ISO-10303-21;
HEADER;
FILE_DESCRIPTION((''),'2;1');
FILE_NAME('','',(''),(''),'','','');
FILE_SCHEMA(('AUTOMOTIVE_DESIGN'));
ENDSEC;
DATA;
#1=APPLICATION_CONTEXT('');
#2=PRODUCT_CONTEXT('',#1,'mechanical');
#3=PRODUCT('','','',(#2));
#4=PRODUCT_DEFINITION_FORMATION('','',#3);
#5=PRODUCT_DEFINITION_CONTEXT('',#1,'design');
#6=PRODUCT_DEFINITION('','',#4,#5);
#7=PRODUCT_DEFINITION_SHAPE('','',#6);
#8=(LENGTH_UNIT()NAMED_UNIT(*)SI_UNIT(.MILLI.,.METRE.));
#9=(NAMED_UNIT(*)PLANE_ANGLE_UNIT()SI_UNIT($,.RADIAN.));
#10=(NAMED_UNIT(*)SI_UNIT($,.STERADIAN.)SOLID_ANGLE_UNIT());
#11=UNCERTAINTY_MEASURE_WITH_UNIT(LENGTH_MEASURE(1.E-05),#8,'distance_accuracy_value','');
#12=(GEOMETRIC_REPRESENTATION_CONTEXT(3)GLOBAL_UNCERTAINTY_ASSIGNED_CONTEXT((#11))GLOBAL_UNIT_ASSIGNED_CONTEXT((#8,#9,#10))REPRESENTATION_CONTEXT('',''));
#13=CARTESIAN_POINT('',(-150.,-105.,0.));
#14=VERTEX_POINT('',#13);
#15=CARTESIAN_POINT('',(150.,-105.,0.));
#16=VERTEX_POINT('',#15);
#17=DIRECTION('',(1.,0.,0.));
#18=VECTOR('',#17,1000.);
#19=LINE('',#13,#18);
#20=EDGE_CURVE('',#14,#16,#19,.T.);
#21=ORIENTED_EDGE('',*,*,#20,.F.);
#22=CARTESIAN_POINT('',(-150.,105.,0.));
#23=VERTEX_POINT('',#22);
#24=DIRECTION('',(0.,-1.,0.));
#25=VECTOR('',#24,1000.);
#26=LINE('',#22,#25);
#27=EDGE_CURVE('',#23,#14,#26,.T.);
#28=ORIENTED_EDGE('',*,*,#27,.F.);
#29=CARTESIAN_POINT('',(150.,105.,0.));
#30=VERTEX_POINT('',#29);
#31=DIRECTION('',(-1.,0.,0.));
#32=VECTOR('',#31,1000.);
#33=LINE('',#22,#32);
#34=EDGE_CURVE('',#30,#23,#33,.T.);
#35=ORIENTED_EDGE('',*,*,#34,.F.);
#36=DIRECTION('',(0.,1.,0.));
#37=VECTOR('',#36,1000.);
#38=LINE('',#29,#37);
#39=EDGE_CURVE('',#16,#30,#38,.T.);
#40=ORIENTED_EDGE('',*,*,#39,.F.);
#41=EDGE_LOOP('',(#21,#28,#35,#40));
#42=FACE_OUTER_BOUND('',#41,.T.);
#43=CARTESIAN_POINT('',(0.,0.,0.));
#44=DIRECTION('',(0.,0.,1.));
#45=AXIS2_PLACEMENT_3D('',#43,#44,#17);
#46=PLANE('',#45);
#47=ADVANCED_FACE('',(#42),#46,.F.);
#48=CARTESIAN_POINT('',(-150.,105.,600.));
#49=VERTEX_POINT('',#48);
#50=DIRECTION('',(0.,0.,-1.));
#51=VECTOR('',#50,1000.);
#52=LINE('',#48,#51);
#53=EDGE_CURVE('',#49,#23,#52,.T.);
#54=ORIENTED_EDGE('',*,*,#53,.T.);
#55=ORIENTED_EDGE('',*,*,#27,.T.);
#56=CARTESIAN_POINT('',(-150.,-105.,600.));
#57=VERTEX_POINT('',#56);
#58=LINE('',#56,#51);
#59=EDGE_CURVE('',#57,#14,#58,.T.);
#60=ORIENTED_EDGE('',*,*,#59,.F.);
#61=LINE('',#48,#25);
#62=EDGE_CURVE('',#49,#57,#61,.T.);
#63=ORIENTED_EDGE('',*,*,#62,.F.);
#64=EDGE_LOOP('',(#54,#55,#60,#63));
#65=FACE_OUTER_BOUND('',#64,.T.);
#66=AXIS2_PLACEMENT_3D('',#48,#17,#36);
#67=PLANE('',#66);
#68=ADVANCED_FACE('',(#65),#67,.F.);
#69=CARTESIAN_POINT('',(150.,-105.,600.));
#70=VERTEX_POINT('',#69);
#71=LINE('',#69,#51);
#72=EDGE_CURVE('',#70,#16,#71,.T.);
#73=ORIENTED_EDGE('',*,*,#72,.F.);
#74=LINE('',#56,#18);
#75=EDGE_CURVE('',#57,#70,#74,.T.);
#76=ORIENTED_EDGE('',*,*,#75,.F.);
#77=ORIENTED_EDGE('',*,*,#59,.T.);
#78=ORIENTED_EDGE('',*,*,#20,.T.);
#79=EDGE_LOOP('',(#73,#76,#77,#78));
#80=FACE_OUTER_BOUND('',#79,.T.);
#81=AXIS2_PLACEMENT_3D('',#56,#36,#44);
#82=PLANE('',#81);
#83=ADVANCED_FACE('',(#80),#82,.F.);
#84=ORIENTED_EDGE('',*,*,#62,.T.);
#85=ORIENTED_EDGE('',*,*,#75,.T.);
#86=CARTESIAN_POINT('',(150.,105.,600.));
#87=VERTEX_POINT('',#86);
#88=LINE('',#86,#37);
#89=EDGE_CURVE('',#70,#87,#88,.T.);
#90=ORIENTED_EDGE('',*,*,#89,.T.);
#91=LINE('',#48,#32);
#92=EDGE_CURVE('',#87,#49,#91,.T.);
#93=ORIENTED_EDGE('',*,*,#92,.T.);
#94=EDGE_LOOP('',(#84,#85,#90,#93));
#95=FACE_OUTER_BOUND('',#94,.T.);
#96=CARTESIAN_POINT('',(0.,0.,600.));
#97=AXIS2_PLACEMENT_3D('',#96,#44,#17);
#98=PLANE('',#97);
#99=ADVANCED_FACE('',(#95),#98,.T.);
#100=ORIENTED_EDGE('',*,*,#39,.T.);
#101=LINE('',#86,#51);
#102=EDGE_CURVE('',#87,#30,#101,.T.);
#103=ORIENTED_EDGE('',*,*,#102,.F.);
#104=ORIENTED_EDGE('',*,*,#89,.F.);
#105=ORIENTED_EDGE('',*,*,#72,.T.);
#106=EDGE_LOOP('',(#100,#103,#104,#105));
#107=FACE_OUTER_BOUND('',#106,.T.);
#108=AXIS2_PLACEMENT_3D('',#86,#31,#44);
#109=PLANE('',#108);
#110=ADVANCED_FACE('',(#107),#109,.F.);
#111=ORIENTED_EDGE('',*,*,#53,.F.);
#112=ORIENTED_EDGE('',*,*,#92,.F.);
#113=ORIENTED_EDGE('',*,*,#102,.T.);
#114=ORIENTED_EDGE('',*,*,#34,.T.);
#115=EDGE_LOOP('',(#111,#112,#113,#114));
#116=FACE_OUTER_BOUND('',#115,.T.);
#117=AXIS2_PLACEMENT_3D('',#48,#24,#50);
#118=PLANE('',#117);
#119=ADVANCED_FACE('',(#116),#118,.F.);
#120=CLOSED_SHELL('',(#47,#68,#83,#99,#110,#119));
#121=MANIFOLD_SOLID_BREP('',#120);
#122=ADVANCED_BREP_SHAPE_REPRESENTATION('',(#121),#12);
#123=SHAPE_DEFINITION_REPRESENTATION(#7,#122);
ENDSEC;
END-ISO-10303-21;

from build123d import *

# Parameters (mm, degrees)
SKETCH_1_W      = 300
SKETCH_1_H      = 210
EXTRUDE_1_DEPTH = 600


with BuildPart() as part:
    # 草图1 → 凸台-拉伸1 (new body)
    with BuildSketch(Plane.XY):
        Rectangle(SKETCH_1_W, SKETCH_1_H)
    extrude(amount=EXTRUDE_1_DEPTH)


solid = part.part
